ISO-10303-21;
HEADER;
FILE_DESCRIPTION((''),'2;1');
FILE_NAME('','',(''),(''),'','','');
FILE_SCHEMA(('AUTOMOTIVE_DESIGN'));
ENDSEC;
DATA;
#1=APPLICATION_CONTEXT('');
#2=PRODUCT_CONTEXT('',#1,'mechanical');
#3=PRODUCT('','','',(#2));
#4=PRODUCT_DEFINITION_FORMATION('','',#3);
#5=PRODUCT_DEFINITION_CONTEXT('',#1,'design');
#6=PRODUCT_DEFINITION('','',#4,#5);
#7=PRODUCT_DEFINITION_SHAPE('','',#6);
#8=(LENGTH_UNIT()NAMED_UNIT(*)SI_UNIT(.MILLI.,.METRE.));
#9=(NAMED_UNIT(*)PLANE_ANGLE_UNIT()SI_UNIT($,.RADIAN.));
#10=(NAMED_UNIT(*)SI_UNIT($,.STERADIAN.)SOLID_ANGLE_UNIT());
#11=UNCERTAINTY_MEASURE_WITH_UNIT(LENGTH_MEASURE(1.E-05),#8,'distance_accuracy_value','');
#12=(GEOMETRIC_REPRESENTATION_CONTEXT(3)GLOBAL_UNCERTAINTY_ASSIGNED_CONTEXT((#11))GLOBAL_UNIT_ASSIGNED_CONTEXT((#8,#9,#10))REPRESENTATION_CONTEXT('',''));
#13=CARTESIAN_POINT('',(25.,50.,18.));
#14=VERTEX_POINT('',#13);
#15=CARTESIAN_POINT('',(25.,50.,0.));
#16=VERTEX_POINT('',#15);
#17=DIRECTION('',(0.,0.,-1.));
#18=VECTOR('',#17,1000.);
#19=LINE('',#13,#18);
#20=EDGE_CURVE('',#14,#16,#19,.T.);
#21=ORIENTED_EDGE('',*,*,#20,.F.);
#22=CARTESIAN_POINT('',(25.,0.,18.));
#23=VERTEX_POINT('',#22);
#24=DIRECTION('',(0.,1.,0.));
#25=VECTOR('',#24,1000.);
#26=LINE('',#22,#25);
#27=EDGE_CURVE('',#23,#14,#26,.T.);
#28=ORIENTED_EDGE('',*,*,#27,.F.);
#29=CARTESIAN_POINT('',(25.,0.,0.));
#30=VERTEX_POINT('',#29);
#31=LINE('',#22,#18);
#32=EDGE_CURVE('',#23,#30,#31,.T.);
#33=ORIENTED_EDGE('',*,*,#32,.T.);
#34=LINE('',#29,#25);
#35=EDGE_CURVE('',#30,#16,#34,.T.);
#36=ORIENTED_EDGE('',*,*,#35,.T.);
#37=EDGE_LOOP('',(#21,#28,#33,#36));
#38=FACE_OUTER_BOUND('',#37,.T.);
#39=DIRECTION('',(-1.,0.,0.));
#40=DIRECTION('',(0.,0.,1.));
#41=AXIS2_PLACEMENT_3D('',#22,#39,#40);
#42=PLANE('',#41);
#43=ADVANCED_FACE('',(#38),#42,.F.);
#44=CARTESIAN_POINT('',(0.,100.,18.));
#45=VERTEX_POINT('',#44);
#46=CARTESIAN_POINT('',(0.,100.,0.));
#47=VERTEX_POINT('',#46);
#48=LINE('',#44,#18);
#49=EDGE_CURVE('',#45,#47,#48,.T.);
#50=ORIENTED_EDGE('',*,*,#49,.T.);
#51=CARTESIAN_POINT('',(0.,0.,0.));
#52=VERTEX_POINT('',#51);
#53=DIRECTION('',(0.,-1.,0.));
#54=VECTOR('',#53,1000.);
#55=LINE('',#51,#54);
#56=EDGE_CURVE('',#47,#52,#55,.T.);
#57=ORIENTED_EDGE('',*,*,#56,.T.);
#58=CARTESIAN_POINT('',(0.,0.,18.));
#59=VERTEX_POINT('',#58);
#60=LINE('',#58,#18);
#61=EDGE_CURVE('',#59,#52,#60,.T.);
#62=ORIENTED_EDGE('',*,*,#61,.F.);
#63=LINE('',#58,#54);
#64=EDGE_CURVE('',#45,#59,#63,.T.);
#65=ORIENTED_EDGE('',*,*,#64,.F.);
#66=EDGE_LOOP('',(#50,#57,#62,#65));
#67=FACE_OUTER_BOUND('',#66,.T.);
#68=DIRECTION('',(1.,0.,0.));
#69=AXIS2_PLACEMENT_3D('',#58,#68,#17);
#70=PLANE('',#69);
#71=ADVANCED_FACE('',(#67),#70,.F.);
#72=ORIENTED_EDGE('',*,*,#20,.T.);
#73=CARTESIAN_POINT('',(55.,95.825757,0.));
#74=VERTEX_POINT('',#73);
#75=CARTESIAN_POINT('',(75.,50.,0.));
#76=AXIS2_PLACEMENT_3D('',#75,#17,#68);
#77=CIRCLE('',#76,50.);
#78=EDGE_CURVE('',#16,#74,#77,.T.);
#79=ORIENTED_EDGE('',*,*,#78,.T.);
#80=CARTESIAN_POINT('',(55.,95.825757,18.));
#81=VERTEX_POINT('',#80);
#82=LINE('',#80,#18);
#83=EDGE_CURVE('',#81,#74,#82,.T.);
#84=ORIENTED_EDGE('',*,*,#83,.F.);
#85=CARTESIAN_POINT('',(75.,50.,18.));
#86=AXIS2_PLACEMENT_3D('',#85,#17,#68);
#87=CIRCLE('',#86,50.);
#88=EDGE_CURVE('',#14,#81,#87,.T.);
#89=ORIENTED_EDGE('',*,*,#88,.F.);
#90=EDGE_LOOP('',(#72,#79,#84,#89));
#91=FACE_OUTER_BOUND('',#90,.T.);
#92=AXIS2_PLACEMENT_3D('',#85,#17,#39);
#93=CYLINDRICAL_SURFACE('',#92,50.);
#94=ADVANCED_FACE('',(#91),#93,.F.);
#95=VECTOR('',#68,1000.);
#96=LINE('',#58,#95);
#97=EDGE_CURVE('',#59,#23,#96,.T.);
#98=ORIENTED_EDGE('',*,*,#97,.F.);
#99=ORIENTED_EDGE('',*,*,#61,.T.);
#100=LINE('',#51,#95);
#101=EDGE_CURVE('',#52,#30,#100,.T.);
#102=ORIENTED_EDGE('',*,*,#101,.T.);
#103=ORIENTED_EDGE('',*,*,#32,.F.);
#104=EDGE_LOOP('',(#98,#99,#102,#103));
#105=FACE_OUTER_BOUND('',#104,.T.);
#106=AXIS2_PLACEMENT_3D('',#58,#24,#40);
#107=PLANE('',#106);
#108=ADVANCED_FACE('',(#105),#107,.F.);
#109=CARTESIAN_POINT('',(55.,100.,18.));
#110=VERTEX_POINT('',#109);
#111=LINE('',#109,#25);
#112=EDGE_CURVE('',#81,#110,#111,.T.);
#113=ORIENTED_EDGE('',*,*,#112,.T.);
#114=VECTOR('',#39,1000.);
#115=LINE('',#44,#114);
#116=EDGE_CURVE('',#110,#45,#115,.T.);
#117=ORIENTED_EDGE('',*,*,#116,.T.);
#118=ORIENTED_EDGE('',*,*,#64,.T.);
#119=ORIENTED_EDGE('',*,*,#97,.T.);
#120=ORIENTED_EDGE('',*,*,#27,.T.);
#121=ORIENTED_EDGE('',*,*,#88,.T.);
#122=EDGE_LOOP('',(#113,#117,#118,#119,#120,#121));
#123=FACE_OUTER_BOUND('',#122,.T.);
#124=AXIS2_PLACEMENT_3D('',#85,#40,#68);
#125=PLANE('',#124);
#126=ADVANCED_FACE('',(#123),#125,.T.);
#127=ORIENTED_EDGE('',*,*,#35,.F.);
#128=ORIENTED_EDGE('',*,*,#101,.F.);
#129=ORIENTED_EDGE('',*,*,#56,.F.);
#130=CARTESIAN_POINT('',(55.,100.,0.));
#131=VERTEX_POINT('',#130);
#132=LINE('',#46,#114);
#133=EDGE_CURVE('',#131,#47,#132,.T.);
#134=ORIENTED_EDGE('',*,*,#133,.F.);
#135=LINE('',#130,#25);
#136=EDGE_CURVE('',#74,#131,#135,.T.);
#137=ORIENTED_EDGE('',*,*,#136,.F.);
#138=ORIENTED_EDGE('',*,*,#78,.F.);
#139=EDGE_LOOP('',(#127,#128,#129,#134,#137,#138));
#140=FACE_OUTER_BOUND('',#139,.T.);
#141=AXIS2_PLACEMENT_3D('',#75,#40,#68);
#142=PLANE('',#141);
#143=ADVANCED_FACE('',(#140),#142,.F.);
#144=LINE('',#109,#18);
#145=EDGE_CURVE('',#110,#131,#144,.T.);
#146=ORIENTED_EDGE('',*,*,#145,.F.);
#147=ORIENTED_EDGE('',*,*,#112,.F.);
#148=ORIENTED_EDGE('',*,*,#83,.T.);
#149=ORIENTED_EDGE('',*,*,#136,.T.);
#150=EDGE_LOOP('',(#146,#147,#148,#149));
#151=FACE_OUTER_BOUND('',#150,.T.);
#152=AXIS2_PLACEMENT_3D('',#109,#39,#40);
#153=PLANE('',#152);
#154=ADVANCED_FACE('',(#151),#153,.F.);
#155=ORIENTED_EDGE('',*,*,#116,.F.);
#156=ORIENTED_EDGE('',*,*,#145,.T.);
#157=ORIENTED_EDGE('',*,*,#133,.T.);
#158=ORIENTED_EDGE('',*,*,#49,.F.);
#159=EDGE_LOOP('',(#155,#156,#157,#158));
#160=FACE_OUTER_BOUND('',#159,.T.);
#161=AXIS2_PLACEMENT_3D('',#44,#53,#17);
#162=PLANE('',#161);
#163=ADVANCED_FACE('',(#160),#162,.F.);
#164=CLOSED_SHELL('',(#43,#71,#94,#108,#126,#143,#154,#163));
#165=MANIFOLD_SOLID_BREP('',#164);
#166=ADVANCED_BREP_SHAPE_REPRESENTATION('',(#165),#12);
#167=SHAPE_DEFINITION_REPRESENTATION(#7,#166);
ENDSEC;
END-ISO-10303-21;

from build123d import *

# Parameters (mm, degrees)
BOSS_EXTRUDE1_DEPTH = 18


with BuildPart() as part:
    # Sketch1 → Boss-Extrude1 (new body)
    with BuildSketch(Plane.XY):
        with BuildLine():
            Line((0, 0), (0, 100))
            Line((0, 100), (55, 100))
            Line((55, 100), (55, 95.82575695))
            ThreePointArc((55, 95.82575695), (33.166998673, 77.386127875), (25, 50))
            Line((25, 50), (25, 0))
            Line((25, 0), (0, 0))
        make_face()
    extrude(amount=BOSS_EXTRUDE1_DEPTH)


solid = part.part
